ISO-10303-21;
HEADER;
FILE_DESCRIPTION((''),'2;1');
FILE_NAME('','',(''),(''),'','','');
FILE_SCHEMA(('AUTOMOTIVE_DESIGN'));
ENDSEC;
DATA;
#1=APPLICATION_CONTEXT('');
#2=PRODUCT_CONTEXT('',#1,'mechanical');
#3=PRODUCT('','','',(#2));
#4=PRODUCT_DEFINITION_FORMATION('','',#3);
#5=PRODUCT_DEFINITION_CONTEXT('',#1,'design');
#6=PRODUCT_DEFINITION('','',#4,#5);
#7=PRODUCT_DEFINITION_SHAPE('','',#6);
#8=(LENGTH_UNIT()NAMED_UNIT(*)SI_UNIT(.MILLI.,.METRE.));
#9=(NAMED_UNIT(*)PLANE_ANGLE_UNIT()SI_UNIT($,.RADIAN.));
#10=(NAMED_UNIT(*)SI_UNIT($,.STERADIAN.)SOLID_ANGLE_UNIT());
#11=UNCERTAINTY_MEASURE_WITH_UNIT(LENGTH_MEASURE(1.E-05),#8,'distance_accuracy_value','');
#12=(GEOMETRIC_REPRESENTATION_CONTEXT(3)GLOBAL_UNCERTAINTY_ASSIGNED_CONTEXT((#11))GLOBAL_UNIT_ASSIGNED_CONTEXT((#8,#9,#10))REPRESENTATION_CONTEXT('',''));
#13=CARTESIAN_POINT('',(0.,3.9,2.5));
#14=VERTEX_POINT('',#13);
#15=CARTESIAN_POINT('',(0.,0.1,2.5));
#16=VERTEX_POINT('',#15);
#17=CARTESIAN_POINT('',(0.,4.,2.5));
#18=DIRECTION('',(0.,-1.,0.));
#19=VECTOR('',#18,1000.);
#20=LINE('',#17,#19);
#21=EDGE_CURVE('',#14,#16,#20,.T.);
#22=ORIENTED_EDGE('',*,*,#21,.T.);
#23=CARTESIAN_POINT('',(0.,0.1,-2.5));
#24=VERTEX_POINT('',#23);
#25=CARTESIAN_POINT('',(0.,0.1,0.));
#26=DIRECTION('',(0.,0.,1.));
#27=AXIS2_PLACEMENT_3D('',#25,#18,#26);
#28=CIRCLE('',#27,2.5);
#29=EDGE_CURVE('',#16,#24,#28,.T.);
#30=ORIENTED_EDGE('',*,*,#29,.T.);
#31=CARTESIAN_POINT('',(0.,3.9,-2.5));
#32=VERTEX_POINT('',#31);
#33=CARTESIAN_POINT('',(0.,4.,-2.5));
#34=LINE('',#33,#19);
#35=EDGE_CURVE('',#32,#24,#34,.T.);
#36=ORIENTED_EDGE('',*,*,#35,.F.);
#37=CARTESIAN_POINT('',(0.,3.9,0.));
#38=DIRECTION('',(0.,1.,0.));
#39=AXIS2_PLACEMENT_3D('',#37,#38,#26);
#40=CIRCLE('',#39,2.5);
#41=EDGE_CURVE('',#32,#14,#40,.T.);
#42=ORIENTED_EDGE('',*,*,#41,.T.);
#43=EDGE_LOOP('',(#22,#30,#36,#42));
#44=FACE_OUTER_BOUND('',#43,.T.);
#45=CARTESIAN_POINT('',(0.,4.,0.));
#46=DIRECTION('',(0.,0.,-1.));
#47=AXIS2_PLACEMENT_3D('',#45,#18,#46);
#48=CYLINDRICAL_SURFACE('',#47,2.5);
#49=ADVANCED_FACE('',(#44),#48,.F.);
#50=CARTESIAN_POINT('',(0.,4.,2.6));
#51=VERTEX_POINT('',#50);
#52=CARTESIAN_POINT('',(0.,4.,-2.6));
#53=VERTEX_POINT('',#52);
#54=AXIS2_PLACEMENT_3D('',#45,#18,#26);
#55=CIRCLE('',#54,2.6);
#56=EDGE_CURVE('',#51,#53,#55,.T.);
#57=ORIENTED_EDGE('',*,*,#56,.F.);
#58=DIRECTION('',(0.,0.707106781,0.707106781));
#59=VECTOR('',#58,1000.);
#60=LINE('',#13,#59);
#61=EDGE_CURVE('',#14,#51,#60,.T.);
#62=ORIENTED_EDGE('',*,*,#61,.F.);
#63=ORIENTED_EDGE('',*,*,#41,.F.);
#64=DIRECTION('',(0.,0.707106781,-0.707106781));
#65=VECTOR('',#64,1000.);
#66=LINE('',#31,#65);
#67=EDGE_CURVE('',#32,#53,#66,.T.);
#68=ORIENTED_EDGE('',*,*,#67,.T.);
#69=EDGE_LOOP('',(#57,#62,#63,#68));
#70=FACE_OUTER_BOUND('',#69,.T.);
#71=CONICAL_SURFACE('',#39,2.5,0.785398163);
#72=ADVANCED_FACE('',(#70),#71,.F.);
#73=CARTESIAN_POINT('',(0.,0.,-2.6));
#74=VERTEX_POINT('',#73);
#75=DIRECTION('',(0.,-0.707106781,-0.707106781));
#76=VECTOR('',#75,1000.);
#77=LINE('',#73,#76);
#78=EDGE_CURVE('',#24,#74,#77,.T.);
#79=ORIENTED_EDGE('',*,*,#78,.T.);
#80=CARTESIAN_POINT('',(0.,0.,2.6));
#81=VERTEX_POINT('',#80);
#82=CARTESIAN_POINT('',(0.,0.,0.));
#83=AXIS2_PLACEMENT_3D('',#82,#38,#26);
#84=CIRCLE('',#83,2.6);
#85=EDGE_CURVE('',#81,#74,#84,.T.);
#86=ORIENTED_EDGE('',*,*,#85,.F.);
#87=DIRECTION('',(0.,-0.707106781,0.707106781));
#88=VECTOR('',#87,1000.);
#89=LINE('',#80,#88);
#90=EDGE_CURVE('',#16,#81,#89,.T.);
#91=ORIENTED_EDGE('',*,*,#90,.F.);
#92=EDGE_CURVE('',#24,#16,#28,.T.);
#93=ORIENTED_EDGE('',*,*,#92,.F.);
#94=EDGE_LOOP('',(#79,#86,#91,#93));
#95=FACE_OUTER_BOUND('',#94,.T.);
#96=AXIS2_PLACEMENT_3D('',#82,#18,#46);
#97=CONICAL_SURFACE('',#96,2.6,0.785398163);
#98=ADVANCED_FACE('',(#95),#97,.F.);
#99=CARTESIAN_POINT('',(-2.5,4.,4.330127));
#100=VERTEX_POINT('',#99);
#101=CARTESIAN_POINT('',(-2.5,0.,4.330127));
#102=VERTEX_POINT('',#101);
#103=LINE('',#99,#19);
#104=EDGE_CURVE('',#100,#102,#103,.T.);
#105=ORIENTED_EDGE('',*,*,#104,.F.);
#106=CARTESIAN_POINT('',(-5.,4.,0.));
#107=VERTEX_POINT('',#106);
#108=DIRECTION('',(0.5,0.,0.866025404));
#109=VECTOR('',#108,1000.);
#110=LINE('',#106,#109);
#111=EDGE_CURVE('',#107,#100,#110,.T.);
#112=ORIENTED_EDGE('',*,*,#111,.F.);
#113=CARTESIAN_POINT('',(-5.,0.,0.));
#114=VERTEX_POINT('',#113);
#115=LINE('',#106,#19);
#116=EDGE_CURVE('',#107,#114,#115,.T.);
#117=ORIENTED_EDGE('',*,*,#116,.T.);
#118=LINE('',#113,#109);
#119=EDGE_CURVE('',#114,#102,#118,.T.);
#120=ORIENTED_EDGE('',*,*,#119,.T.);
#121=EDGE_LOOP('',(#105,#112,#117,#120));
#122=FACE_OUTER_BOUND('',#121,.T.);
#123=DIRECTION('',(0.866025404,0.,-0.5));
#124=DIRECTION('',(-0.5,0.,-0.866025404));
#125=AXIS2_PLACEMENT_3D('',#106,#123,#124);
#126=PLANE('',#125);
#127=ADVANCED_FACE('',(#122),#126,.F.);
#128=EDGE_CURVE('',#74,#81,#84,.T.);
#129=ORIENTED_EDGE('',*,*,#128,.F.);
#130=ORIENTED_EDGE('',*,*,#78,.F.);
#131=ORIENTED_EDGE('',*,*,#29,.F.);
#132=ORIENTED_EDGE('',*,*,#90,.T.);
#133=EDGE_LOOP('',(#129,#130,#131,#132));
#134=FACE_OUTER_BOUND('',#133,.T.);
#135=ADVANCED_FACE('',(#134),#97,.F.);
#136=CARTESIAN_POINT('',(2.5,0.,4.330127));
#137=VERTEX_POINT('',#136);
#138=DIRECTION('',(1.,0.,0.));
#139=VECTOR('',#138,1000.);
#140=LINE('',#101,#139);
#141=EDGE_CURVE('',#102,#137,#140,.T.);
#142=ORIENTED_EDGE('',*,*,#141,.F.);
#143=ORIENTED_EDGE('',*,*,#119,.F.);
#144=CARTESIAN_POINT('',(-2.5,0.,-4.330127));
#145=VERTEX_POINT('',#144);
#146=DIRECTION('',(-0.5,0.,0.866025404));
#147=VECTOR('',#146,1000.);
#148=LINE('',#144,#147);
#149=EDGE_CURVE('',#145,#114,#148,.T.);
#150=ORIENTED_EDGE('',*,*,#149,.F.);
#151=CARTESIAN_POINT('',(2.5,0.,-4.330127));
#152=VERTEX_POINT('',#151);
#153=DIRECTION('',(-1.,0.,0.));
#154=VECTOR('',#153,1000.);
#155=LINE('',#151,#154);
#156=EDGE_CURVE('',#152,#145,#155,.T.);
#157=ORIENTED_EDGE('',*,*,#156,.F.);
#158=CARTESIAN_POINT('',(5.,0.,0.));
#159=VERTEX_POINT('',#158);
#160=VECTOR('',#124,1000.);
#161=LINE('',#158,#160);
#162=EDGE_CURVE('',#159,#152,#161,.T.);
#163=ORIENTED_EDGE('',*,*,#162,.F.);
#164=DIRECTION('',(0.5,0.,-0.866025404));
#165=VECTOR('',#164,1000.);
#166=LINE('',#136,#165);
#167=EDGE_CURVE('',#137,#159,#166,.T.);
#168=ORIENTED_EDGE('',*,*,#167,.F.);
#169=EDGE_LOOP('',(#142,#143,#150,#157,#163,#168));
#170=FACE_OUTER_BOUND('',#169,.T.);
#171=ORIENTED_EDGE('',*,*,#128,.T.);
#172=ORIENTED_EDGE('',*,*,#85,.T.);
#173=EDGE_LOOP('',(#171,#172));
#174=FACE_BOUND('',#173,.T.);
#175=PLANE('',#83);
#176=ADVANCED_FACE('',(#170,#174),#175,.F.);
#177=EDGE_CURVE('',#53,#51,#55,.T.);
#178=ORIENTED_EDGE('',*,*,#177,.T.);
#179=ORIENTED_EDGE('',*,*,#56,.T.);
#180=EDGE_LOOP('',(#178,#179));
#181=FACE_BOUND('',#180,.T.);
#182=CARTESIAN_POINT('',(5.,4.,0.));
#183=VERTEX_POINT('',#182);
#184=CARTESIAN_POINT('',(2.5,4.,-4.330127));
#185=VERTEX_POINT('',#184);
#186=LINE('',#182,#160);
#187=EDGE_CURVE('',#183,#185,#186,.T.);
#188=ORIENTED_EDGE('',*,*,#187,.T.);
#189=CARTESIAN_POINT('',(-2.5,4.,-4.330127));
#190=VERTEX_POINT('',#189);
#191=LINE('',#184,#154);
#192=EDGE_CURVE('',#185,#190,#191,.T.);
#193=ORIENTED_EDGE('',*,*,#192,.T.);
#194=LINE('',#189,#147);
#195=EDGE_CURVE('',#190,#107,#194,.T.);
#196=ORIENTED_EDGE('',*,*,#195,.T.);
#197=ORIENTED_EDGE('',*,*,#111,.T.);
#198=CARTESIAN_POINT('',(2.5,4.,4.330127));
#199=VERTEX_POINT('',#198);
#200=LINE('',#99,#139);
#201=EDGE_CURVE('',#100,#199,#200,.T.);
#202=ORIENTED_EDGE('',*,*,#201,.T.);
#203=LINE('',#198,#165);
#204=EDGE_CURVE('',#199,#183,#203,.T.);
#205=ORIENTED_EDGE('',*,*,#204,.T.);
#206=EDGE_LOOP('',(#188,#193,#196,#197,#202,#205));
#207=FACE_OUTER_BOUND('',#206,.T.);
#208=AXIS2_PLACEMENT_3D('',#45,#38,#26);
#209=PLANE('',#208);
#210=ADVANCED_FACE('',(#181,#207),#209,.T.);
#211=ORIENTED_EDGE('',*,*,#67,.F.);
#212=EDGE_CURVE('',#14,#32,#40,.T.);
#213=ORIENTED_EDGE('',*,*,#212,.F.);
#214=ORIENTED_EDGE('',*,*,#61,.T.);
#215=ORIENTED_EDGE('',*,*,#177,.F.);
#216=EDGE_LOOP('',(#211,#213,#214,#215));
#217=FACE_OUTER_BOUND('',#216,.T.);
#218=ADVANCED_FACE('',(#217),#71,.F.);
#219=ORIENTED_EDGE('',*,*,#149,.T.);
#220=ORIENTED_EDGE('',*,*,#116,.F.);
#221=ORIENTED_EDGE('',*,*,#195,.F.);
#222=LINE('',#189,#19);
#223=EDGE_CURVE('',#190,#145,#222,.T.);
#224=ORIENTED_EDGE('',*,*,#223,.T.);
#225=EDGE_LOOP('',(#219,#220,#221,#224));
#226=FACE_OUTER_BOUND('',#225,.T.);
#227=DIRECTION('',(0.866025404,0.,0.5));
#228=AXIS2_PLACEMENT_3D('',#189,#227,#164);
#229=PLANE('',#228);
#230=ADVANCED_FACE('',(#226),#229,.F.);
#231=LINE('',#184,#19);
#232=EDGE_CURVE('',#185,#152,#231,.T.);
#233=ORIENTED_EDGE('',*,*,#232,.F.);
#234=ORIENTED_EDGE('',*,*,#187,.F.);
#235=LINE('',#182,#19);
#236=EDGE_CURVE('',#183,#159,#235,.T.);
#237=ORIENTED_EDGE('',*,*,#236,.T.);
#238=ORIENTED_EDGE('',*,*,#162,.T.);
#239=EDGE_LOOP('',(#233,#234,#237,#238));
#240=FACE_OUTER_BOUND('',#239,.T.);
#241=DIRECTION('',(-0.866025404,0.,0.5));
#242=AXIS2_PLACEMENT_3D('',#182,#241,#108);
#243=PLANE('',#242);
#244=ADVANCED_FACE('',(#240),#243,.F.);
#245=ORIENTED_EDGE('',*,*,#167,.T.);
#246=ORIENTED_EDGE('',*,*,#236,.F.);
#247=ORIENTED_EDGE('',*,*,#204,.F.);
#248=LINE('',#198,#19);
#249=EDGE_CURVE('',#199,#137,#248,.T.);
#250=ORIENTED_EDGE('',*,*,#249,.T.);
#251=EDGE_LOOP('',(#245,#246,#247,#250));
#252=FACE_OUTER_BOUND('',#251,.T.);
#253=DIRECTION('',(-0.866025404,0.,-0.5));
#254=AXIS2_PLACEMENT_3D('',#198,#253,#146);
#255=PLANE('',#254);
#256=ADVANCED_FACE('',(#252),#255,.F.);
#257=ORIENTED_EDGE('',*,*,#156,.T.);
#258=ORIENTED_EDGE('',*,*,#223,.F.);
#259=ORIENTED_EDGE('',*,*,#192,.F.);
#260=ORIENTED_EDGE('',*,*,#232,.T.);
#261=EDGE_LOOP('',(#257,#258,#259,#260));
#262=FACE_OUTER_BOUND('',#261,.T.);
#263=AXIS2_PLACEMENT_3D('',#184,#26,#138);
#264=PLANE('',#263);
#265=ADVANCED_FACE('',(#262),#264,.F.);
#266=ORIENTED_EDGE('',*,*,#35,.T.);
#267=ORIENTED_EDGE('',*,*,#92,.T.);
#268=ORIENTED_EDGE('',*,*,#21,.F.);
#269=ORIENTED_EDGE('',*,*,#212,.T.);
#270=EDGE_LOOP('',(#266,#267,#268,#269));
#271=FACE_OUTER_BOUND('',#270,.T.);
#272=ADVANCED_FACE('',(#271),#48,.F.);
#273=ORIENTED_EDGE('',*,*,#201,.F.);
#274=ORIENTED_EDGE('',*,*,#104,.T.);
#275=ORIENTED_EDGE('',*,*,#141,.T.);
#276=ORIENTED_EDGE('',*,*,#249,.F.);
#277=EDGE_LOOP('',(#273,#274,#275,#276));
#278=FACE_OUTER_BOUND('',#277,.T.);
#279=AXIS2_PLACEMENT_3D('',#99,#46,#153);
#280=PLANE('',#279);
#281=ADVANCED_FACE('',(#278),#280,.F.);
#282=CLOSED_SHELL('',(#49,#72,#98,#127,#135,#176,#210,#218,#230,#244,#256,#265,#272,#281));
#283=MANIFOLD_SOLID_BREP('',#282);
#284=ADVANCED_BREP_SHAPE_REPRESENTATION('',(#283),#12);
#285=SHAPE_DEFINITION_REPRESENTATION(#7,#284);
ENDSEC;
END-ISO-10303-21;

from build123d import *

# Parameters (mm, degrees)
SKETCH1_R           = 2.5
BOSS_EXTRUDE1_DEPTH = 4
CHAMFER1_SIZE       = 0.1


with BuildPart() as part:
    # Sketch1 → Boss-Extrude1 (new body)
    with BuildSketch(Plane(origin=(0, 0, 0), x_dir=(1, 0, 0), z_dir=(0, 1, 0))):
        Polygon((2.5, -4.330127019), (5, 0), (2.5, 4.330127019), (-2.5, 4.330127019), (-5, 0), (-2.5, -4.330127019), align=None)
        with Locations(Location((0, 0, 0), (0, 0, 270))):
            Circle(SKETCH1_R, mode=Mode.SUBTRACT)
    extrude(amount=BOSS_EXTRUDE1_DEPTH)

    # Chamfer1
    chamfer1_edges = [part.edges().sort_by_distance(p)[0] for p in [
        (0, 0, -2.5),
        (0, 4, -2.5),
    ]]
    chamfer(chamfer1_edges, length=CHAMFER1_SIZE)


solid = part.part
